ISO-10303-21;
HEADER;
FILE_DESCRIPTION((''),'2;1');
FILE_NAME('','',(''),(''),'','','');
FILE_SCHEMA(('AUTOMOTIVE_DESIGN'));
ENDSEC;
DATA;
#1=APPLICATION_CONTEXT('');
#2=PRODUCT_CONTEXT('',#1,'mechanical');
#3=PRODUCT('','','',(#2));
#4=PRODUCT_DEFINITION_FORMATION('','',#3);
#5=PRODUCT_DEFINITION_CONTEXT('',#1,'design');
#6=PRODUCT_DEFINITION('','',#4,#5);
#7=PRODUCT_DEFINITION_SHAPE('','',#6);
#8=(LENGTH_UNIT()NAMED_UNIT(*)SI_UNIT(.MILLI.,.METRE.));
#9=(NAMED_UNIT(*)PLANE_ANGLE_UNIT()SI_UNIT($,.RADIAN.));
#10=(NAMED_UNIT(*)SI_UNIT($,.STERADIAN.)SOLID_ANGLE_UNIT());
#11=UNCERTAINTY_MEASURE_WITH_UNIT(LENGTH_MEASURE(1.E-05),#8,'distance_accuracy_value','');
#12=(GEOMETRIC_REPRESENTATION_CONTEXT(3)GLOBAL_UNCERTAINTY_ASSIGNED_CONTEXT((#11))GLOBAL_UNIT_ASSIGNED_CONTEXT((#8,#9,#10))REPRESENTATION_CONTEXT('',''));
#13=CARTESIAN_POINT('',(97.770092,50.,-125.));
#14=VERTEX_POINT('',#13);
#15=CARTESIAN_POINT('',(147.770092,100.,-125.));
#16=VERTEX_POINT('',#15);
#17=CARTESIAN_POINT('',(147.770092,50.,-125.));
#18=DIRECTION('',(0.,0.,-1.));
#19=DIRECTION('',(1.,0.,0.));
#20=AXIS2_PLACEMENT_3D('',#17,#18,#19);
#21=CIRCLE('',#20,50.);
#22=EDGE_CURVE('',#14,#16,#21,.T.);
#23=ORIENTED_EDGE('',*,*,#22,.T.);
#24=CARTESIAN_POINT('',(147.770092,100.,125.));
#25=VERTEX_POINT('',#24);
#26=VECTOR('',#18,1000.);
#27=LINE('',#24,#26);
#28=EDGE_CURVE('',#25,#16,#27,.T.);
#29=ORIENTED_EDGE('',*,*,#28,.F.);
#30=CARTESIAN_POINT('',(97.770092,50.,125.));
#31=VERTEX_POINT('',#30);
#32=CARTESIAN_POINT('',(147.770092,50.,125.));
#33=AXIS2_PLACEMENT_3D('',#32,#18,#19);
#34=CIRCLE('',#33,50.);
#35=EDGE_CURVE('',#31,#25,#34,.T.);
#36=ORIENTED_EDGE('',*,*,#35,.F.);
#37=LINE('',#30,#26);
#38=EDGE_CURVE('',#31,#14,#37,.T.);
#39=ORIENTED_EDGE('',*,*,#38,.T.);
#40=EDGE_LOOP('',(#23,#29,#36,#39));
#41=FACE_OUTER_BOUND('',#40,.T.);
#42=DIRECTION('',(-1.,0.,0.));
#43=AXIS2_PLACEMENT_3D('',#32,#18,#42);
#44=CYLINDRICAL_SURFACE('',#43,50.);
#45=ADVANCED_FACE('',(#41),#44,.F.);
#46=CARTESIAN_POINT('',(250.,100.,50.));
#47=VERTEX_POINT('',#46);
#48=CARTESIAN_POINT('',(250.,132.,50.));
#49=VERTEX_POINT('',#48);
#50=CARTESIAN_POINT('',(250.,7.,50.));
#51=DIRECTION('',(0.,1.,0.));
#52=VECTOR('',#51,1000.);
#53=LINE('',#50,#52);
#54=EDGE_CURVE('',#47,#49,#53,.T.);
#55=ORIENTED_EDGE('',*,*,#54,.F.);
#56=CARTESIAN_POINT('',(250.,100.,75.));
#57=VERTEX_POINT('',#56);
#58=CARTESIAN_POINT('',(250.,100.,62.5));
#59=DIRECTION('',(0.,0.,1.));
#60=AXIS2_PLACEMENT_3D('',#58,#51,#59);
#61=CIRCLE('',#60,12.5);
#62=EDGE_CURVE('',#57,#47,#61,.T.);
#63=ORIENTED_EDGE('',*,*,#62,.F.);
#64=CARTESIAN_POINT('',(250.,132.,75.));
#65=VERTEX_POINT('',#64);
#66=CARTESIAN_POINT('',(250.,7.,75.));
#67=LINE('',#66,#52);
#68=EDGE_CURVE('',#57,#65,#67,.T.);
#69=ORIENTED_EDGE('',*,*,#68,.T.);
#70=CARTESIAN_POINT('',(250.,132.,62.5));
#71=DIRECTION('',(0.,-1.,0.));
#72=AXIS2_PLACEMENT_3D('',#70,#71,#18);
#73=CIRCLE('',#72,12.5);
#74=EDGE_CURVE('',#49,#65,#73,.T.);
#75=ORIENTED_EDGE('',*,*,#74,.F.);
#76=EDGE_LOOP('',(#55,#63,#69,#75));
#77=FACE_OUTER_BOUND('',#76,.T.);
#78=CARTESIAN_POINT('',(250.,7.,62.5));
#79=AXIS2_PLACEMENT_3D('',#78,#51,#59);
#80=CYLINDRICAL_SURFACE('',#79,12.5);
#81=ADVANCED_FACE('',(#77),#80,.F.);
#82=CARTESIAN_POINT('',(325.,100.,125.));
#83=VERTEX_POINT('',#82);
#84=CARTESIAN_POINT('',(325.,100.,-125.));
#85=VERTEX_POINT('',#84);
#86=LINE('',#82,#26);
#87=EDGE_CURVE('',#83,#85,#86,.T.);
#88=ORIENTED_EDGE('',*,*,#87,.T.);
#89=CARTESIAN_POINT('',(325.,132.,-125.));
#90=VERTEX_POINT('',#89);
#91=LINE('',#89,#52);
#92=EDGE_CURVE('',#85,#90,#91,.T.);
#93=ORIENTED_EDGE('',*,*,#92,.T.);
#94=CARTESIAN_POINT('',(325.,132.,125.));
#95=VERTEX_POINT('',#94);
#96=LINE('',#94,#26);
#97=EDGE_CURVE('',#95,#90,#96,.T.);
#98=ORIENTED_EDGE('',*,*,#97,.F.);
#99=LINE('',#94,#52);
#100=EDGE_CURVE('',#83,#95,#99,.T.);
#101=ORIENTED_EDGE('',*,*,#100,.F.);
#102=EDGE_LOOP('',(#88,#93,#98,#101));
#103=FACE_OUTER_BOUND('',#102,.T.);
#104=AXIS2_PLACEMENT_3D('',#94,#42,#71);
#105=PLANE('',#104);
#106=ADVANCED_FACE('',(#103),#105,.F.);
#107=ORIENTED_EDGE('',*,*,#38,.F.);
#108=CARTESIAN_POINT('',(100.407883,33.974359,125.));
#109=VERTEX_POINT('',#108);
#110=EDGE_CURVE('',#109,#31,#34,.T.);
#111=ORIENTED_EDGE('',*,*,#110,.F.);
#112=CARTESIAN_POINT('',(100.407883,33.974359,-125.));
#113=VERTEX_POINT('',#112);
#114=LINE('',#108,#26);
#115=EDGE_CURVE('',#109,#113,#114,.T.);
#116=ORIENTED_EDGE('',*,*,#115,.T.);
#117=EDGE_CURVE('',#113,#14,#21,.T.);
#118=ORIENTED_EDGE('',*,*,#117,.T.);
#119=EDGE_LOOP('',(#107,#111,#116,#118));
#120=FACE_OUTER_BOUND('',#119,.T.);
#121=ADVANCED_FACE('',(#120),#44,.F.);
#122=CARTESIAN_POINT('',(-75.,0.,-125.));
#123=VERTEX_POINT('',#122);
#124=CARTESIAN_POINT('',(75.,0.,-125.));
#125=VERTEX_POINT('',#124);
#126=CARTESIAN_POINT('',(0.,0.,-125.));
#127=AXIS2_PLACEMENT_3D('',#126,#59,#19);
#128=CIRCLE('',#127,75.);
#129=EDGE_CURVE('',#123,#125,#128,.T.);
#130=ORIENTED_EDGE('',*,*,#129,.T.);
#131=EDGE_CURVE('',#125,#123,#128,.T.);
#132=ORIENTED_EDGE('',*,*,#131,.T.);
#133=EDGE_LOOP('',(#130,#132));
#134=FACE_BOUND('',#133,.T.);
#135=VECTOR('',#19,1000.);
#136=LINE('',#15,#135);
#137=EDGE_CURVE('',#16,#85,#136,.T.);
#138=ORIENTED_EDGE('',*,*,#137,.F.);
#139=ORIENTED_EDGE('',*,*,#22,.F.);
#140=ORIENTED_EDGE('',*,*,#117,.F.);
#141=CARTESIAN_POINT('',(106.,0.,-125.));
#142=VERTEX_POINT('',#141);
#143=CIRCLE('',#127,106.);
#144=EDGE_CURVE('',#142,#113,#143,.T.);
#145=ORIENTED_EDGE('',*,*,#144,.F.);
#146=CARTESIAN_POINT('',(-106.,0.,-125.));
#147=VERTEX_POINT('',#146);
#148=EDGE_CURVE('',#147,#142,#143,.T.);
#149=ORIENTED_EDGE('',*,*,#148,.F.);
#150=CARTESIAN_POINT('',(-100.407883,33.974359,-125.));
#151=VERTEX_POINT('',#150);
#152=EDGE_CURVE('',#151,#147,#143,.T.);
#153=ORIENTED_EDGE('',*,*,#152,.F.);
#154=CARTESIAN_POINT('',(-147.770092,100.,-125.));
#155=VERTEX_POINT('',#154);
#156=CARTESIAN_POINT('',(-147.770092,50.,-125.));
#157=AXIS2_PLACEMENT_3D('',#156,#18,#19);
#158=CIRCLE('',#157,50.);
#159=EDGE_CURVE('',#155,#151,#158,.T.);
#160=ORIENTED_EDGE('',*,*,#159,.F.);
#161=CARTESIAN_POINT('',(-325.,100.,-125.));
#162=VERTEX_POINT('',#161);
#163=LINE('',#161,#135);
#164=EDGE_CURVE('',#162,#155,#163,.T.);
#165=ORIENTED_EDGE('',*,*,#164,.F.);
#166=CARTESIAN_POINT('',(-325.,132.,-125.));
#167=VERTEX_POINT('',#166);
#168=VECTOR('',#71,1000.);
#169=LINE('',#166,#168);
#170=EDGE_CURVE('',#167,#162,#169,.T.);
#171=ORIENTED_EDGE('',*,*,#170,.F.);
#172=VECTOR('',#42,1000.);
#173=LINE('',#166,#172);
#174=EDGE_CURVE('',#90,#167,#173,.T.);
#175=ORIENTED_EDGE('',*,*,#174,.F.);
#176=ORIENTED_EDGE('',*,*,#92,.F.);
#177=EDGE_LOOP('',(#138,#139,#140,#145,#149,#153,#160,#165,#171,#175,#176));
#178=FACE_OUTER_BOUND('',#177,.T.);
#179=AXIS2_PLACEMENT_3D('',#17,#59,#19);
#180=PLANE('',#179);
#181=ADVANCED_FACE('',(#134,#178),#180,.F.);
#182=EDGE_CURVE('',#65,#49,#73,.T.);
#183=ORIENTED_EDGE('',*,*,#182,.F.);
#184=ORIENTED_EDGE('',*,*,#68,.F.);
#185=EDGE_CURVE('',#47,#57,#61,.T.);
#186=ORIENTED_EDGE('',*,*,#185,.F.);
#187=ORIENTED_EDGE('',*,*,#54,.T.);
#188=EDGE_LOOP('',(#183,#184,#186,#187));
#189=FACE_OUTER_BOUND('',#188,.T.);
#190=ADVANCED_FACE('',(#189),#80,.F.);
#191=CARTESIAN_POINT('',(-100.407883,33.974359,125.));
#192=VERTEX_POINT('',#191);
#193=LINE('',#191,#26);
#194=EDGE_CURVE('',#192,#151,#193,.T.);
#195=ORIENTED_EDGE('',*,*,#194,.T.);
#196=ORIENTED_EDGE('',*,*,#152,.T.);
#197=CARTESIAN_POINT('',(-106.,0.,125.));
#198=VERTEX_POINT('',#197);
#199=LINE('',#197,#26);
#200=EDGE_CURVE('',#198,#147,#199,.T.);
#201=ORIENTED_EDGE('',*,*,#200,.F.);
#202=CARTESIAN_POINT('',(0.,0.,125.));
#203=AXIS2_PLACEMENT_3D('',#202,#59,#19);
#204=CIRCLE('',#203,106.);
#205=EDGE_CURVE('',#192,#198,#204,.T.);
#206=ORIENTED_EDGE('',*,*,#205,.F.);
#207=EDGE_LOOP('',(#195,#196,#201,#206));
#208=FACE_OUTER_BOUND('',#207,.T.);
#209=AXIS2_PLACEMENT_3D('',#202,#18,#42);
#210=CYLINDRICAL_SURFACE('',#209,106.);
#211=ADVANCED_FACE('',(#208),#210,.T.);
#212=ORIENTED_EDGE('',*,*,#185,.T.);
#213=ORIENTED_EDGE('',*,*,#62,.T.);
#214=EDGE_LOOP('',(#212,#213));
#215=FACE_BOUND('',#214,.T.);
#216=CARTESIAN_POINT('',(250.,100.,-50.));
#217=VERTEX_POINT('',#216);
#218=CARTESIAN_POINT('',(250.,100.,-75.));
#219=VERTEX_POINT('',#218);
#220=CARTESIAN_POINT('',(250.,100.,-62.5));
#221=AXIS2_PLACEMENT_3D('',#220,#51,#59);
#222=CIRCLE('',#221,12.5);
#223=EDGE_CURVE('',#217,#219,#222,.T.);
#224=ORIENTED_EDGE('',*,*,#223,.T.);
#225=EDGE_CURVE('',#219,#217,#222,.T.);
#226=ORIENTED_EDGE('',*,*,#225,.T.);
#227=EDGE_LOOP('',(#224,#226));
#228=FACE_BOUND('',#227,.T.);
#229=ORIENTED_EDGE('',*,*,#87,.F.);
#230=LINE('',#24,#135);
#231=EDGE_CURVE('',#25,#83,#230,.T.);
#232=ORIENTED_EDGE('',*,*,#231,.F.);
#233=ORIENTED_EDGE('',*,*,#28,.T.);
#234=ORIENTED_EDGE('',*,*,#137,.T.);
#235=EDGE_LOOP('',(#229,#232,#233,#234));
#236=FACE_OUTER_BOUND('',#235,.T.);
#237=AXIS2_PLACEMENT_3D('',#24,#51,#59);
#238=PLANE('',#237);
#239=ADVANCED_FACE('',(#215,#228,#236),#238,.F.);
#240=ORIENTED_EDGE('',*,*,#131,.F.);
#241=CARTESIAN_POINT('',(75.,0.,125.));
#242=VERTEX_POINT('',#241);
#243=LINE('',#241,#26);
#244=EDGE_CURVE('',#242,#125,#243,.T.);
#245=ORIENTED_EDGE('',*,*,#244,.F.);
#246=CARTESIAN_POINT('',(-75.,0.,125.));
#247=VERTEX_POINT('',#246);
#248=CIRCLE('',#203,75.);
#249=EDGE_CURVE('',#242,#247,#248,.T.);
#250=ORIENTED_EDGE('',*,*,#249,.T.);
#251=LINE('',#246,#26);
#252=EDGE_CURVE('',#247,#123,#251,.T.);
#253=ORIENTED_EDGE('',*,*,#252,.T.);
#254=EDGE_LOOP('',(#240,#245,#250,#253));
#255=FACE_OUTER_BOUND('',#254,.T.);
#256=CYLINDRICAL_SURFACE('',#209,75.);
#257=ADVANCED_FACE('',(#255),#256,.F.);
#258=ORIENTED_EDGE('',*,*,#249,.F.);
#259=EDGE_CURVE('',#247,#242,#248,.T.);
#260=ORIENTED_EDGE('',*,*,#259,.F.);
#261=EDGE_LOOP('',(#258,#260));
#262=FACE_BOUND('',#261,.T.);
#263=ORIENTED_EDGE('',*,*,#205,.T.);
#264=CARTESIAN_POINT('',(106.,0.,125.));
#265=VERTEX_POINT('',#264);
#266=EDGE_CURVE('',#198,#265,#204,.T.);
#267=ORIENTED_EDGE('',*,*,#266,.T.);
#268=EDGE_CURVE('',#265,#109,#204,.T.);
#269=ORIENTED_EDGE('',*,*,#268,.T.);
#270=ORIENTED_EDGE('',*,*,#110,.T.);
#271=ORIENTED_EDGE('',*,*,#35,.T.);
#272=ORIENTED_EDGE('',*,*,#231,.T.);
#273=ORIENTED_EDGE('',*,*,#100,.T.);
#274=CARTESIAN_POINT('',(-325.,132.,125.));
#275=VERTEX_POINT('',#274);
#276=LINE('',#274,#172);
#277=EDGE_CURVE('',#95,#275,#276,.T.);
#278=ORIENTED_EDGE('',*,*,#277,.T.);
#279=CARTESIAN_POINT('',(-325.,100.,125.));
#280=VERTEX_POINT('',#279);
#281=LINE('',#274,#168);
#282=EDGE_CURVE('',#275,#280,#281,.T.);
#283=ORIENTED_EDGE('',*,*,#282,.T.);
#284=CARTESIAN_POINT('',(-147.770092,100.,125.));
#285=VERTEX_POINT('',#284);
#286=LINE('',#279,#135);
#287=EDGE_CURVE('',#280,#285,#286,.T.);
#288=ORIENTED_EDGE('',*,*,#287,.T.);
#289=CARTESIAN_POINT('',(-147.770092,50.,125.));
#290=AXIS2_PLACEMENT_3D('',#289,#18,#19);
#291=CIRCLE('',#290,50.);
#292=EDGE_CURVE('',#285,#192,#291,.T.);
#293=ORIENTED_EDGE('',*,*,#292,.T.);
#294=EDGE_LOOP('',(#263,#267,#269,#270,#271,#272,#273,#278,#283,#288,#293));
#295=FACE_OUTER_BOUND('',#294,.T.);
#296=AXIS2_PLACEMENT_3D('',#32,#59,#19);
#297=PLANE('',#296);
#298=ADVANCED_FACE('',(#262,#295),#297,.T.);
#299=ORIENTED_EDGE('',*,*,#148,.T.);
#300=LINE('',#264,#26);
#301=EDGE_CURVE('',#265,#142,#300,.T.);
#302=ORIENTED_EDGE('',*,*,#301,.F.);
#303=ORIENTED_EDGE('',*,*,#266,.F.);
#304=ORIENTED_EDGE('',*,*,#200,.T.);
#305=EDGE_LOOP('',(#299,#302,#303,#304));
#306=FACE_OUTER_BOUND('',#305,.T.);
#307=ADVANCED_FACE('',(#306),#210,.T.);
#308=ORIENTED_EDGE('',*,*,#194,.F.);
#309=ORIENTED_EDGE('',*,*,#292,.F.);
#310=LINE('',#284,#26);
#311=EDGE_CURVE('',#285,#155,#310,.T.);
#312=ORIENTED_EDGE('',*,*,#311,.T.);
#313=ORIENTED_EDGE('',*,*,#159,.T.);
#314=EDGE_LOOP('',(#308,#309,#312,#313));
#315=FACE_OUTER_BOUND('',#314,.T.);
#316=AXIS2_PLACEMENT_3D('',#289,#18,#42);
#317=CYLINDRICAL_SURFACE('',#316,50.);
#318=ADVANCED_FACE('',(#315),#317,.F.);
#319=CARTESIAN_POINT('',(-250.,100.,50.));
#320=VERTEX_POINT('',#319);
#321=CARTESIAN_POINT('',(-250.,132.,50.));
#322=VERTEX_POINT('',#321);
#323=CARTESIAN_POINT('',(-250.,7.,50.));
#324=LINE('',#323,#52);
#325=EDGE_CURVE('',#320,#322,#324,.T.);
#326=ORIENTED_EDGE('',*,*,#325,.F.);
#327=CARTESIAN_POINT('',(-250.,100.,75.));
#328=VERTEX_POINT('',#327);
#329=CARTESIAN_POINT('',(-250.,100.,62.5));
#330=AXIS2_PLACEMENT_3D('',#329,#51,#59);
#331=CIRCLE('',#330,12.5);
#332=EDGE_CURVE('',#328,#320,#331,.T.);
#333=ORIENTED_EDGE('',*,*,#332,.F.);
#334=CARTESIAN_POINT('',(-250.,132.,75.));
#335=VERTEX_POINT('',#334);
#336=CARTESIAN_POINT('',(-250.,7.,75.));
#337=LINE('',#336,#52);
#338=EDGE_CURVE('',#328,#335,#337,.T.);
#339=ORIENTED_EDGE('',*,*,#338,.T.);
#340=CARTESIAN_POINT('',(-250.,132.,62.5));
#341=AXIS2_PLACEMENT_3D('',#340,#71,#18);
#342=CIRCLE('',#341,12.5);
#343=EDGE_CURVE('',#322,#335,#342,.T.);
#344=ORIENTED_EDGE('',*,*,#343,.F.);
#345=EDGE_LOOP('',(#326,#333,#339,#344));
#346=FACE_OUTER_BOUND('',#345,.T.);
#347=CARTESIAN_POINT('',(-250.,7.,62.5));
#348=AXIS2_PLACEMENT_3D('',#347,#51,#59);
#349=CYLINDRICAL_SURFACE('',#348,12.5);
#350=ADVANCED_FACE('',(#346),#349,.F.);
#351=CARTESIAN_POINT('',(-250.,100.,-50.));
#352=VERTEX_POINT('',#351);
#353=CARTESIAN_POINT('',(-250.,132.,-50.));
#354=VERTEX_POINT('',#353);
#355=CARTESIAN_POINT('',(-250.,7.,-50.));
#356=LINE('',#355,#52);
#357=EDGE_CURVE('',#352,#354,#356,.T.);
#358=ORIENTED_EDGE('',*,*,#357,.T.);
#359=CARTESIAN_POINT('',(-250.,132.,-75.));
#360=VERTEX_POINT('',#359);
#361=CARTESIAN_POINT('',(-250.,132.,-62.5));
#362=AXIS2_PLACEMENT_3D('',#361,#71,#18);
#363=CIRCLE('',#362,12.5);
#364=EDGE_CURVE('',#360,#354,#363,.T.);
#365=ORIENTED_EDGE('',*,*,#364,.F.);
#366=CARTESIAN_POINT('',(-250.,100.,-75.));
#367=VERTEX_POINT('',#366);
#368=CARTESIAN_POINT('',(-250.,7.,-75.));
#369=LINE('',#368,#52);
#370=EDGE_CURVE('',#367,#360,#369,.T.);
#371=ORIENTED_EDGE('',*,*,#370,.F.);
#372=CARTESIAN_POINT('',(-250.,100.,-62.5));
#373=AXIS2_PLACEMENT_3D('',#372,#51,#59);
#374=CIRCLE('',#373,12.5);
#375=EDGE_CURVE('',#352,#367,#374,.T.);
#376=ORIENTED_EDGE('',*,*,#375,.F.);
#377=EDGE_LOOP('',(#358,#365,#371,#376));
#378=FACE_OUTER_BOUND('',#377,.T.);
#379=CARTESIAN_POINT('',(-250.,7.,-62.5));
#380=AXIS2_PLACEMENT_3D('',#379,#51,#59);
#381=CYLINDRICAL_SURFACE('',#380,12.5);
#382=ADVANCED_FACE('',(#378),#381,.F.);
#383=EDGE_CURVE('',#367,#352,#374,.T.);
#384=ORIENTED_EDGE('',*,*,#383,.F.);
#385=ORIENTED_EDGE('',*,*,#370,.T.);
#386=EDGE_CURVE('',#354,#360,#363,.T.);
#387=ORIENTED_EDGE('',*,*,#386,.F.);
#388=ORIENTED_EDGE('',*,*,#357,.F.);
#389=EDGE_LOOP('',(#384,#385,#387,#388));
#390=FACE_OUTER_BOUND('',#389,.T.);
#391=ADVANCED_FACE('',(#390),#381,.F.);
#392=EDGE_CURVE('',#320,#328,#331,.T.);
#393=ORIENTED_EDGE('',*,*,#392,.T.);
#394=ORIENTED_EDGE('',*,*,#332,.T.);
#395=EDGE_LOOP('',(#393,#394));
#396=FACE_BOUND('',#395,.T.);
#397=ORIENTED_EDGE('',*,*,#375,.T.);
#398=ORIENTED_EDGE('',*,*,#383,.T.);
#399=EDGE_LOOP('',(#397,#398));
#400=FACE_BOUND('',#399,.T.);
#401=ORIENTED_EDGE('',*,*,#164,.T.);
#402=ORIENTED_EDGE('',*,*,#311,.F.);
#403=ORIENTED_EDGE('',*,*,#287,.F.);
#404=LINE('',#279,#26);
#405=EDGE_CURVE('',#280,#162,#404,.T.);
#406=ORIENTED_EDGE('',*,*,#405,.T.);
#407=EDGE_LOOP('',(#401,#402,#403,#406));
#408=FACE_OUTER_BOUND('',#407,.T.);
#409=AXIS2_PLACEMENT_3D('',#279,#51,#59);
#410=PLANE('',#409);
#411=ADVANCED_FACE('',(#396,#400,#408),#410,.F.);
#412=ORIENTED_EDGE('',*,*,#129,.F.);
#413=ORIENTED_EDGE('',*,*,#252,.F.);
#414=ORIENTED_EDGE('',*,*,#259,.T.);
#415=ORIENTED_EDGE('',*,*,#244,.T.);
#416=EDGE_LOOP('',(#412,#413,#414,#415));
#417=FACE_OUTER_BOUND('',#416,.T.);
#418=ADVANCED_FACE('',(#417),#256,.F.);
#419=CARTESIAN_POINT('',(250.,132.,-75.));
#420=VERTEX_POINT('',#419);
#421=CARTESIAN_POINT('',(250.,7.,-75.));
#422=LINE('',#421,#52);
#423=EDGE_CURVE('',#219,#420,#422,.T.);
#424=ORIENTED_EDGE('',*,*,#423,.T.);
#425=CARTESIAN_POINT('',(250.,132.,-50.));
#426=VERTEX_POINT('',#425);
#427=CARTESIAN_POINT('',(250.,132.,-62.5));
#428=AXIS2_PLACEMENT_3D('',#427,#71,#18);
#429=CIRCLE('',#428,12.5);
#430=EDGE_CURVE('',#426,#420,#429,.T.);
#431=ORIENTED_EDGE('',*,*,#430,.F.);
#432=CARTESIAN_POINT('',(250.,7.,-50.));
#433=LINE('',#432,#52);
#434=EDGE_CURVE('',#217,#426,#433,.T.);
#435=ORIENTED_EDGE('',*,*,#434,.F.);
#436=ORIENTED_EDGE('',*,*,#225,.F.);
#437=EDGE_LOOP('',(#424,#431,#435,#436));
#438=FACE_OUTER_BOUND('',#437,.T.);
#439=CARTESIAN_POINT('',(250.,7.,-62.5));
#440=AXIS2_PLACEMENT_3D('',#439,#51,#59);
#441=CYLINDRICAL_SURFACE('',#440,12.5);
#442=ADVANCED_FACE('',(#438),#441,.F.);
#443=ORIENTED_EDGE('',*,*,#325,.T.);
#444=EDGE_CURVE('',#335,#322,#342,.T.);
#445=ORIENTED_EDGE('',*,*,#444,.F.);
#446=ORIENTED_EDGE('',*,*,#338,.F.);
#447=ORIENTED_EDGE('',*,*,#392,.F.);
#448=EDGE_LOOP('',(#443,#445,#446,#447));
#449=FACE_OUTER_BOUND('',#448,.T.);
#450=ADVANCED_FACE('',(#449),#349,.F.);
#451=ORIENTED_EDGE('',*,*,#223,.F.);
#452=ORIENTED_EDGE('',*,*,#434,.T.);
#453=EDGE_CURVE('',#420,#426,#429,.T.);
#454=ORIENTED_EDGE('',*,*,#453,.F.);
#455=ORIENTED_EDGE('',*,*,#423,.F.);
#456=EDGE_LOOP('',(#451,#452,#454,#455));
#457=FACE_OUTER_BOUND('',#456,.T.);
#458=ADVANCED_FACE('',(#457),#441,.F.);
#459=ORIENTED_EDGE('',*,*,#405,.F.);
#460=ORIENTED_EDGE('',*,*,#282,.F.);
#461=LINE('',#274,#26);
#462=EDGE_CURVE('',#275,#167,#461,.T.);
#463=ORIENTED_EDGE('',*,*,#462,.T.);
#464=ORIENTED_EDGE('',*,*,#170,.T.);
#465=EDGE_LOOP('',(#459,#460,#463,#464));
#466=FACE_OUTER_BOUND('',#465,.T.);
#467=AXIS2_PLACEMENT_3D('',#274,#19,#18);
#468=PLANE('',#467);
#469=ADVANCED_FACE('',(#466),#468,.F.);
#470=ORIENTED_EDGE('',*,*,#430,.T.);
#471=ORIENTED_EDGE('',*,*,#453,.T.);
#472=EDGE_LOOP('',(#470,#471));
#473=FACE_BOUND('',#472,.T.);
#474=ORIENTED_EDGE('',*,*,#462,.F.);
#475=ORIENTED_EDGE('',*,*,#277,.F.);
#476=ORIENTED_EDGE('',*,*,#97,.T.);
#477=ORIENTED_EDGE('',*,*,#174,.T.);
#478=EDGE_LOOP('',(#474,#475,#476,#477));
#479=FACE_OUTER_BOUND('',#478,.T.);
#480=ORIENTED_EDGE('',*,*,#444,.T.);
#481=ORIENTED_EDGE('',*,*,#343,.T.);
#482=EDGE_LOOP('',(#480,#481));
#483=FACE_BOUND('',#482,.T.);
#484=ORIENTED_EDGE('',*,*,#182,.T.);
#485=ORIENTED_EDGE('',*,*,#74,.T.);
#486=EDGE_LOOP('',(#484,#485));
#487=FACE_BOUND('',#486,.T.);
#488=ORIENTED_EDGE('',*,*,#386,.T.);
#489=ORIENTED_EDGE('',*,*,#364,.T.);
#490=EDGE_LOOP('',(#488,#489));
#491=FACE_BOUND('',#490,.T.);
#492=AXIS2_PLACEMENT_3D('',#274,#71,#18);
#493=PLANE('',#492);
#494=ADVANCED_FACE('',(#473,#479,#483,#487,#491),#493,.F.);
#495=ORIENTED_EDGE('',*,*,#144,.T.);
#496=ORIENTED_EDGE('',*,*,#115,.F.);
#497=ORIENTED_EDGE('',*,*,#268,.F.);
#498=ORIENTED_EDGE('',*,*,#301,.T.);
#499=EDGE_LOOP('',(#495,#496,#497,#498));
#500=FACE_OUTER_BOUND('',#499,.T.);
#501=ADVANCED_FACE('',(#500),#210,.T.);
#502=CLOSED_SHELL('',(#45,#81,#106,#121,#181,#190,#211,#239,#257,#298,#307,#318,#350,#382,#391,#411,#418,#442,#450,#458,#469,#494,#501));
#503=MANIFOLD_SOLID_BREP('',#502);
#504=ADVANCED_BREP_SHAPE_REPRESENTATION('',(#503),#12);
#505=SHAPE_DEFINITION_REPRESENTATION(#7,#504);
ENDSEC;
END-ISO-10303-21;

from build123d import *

# Parameters (mm, degrees)
PIVOT_BRACKET_PROFILE_R  = 75
PIVOT_BRACKET_BODY_DEPTH = 125
MOUNTING_HOLES_SKETCH_R  = 12.5
MOUNTING_HOLES_4X_DEPTH  = 125


with BuildPart() as part:
    # Pivot Bracket Profile → Pivot Bracket Body (new, symmetric)
    with BuildSketch(Plane.XY):
        with BuildLine():
            Line((147.770091697, 100), (325, 100))
            Line((325, 100), (325, 132))
            Line((325, 132), (-325, 132))
            Line((-325, 132), (-325, 100))
            Line((-325, 100), (-147.770091697, 100))
            ThreePointArc((-147.770091697, 100), (-107.142009959, 79.143763902), (-100.407882819, 33.974358974))
            ThreePointArc((-100.407882819, 33.974358974), (0, -106), (100.407882819, 33.974358974))
            ThreePointArc((100.407882819, 33.974358974), (107.142009959, 79.143763902), (147.770091697, 100))
        make_face()
        Circle(PIVOT_BRACKET_PROFILE_R, mode=Mode.SUBTRACT)
    extrude(amount=PIVOT_BRACKET_BODY_DEPTH, both=True)

    # Mounting Holes Sketch → Mounting Holes 4x (cut, symmetric)
    with BuildSketch(Plane(origin=(0, 132, 0), x_dir=(1, 0, 0), z_dir=(0, 1, 0))):
        with Locations(Location((-250, 62.5, 0), (0, 0, 270))):
            Circle(MOUNTING_HOLES_SKETCH_R)
        with Locations(Location((-250, -62.5, 0), (0, 0, 270))):
            Circle(MOUNTING_HOLES_SKETCH_R)
        with Locations(Location((250, -62.5, 0), (0, 0, 270))):
            Circle(MOUNTING_HOLES_SKETCH_R)
        with Locations(Location((250, 62.5, 0), (0, 0, 270))):
            Circle(MOUNTING_HOLES_SKETCH_R)
    extrude(amount=MOUNTING_HOLES_4X_DEPTH, both=True, mode=Mode.SUBTRACT)


solid = part.part
